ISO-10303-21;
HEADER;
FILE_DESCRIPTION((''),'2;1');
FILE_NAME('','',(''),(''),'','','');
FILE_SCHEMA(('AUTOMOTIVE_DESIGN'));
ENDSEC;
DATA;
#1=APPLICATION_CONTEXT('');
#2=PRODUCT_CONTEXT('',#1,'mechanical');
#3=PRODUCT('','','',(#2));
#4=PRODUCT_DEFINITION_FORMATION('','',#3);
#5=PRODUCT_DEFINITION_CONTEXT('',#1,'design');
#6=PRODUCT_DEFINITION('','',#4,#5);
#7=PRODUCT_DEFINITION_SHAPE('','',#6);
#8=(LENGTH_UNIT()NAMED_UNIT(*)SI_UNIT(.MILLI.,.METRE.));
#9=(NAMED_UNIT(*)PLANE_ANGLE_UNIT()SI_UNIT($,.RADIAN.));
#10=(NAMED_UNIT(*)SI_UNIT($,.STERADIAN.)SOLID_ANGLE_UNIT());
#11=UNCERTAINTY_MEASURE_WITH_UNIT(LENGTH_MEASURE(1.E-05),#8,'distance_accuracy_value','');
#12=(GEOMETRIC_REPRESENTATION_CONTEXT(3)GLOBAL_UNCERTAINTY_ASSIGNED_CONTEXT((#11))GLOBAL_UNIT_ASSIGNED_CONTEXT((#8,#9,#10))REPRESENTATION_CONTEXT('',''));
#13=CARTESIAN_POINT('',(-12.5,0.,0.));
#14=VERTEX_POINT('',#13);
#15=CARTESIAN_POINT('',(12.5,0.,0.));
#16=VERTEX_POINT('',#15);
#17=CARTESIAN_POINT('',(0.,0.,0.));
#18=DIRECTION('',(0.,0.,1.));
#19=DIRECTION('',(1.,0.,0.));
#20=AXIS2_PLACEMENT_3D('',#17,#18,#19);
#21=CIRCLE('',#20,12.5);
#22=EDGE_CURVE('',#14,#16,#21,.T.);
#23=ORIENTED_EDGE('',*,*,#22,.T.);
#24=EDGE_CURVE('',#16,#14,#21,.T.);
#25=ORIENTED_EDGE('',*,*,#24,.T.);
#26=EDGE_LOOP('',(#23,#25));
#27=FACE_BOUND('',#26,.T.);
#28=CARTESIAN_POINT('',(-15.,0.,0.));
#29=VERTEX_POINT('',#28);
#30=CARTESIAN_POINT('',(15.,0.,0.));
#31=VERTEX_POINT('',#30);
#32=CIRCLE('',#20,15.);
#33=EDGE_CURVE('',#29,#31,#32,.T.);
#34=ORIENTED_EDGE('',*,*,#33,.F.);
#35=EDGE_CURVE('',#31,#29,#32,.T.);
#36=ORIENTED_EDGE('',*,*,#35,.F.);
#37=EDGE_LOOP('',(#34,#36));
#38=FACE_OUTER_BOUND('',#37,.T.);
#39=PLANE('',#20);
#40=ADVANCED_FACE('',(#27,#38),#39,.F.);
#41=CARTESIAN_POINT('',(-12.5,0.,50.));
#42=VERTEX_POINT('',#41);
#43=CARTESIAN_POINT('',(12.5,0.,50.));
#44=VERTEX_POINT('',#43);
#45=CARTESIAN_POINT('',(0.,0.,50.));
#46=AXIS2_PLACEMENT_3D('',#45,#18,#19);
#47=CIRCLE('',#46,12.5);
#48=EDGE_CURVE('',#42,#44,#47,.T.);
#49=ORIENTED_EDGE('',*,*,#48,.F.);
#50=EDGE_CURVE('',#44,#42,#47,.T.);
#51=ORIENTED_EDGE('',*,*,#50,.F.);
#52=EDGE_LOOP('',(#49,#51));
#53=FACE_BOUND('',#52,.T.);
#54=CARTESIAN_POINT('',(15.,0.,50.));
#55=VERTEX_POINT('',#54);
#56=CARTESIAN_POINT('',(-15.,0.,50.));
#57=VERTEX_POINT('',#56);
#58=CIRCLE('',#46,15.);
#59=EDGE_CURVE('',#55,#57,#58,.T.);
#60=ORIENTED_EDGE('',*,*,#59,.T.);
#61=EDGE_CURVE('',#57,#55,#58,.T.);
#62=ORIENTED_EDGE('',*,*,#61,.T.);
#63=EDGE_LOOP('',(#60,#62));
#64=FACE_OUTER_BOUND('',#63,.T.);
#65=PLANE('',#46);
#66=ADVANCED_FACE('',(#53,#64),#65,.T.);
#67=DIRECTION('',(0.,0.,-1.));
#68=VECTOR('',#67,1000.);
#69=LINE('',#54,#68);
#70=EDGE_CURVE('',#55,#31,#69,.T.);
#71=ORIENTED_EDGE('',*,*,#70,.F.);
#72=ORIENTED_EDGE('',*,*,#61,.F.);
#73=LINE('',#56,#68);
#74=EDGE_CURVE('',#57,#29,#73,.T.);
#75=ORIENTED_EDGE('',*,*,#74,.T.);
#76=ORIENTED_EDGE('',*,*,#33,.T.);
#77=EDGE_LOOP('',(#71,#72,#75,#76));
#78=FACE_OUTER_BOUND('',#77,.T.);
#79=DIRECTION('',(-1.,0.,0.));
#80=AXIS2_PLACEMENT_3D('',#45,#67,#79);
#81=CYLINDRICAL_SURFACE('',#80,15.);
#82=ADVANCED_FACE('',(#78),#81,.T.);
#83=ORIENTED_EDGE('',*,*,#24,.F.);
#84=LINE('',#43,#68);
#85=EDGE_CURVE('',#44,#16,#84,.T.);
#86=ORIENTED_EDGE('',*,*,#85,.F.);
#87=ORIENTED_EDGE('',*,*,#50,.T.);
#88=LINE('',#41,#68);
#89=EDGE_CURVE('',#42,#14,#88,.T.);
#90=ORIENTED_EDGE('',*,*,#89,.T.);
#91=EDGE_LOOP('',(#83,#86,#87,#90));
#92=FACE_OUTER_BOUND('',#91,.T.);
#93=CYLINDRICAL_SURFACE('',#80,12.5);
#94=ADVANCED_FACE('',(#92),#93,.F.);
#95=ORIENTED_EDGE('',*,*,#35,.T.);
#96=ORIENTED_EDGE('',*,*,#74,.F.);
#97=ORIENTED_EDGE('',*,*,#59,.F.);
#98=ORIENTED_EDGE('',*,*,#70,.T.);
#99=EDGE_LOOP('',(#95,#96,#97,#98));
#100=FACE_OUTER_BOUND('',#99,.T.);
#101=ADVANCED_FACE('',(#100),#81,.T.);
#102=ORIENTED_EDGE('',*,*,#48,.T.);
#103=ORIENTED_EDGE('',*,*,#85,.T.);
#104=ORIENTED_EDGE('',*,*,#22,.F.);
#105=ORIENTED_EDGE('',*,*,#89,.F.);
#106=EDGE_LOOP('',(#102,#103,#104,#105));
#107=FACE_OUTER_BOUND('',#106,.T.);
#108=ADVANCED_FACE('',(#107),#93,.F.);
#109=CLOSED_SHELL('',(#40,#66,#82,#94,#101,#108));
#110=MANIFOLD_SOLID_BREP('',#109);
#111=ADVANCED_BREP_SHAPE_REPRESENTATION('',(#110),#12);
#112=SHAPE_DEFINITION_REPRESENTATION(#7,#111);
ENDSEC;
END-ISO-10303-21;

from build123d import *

# Parameters (mm, degrees)
SKETCH1_R           = 15
SKETCH1_R_2         = 12.5
BOSS_EXTRUDE1_DEPTH = 50


with BuildPart() as part:
    # Sketch1 → Boss-Extrude1 (new body)
    with BuildSketch(Plane.XY):
        with Locations(Location((0, 0, 0), (0, 0, 180))):
            Circle(SKETCH1_R)
        with Locations(Location((0, 0, 0), (0, 0, 180))):
            Circle(SKETCH1_R_2, mode=Mode.SUBTRACT)
    extrude(amount=BOSS_EXTRUDE1_DEPTH)


solid = part.part
